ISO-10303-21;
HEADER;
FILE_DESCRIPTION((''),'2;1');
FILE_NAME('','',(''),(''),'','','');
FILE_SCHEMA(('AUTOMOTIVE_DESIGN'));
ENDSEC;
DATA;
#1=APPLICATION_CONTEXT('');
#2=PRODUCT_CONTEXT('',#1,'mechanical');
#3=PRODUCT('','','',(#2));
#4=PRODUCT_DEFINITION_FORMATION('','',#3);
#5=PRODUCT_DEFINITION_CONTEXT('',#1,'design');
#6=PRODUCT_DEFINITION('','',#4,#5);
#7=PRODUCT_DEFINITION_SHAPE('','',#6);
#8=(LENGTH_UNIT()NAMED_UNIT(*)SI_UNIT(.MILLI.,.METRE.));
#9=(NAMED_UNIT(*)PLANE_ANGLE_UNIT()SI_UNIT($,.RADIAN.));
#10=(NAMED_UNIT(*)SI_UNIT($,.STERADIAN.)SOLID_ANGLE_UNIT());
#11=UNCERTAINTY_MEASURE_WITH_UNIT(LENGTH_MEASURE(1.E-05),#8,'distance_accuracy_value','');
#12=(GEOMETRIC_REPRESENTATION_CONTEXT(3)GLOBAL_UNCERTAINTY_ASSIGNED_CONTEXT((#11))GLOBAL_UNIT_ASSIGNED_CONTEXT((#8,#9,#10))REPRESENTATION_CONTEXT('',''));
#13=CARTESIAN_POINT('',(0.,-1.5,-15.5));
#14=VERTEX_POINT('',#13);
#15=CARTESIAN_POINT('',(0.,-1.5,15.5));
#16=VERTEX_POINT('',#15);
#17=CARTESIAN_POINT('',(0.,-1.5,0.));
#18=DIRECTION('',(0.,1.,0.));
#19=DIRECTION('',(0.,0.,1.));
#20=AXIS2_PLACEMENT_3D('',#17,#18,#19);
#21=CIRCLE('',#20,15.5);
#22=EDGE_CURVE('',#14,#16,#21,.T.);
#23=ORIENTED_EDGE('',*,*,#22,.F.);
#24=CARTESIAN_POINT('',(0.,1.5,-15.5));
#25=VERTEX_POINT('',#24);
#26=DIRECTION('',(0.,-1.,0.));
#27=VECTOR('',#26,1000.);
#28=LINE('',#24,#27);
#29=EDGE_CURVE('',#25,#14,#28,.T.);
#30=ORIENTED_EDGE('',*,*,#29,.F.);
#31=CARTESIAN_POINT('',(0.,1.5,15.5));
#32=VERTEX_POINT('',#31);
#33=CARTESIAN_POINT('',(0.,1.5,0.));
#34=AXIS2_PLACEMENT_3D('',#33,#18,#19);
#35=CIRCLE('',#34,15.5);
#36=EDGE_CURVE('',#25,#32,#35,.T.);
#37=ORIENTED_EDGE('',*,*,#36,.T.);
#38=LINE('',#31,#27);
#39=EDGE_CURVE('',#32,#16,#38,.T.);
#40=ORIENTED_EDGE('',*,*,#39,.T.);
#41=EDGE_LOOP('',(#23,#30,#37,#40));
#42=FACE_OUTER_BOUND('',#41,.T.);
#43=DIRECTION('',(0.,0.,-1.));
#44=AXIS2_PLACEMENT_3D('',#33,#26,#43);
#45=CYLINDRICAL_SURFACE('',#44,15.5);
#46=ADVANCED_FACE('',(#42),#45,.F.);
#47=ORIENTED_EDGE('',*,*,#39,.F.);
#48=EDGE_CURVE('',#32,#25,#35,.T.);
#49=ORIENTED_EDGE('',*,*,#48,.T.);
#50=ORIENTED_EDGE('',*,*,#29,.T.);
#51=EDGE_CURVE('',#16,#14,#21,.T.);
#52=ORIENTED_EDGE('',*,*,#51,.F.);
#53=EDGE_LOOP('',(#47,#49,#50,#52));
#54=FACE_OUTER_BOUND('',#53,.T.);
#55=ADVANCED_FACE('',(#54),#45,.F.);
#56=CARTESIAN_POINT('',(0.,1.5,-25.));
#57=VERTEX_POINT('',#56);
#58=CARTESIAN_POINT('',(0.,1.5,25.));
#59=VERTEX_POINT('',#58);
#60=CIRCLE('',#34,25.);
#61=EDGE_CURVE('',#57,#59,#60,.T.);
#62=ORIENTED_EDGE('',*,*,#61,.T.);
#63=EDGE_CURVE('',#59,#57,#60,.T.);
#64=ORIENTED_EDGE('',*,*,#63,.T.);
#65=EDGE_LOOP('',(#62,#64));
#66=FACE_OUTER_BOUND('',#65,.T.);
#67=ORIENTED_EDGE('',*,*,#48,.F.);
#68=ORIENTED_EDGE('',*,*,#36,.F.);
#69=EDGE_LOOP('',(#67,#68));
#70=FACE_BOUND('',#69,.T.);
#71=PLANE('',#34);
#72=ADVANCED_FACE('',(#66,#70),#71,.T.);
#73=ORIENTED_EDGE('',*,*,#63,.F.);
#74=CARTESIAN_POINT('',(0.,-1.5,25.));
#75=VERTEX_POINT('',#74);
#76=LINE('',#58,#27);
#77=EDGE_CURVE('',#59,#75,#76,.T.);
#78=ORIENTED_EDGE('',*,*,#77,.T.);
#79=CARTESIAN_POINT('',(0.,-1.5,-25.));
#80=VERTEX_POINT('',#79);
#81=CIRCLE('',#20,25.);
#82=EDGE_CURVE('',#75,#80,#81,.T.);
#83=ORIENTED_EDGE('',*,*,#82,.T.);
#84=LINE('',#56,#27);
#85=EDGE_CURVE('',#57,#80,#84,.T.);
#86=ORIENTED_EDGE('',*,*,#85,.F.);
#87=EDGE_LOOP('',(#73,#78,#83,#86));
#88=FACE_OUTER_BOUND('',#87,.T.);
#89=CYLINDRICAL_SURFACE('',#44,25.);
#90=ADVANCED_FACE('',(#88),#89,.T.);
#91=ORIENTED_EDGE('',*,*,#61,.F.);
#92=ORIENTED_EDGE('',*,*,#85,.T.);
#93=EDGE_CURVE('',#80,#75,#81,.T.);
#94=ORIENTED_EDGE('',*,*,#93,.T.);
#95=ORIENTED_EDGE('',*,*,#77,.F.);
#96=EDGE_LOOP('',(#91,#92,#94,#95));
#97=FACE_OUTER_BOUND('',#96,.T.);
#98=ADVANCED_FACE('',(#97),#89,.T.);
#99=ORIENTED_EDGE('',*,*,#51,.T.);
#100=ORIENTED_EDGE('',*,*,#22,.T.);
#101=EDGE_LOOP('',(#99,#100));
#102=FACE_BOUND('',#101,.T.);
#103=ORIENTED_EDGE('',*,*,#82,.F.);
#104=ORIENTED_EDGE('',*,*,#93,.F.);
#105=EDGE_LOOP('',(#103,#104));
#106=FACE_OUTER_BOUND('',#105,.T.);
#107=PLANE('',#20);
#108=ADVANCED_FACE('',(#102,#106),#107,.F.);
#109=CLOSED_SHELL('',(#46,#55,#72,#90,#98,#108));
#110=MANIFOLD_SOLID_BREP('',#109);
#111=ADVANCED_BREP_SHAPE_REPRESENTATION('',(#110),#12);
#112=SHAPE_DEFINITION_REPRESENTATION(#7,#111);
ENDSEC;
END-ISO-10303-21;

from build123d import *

# Parameters (mm, degrees)
SKETCH_1_R      = 25
SKETCH_1_R_2    = 15.5
EXTRUDE_1_DEPTH = 1.5


with BuildPart() as part:
    # 草图1 → 凸台-拉伸1 (new, symmetric)
    with BuildSketch(Plane(origin=(0, 0, 0), x_dir=(1, 0, 0), z_dir=(0, 1, 0))):
        with Locations(Location((0, 0, 0), (0, 0, 270))):
            Circle(SKETCH_1_R)
        with Locations(Location((0, 0, 0), (0, 0, 270))):
            Circle(SKETCH_1_R_2, mode=Mode.SUBTRACT)
    extrude(amount=EXTRUDE_1_DEPTH, both=True)


solid = part.part
